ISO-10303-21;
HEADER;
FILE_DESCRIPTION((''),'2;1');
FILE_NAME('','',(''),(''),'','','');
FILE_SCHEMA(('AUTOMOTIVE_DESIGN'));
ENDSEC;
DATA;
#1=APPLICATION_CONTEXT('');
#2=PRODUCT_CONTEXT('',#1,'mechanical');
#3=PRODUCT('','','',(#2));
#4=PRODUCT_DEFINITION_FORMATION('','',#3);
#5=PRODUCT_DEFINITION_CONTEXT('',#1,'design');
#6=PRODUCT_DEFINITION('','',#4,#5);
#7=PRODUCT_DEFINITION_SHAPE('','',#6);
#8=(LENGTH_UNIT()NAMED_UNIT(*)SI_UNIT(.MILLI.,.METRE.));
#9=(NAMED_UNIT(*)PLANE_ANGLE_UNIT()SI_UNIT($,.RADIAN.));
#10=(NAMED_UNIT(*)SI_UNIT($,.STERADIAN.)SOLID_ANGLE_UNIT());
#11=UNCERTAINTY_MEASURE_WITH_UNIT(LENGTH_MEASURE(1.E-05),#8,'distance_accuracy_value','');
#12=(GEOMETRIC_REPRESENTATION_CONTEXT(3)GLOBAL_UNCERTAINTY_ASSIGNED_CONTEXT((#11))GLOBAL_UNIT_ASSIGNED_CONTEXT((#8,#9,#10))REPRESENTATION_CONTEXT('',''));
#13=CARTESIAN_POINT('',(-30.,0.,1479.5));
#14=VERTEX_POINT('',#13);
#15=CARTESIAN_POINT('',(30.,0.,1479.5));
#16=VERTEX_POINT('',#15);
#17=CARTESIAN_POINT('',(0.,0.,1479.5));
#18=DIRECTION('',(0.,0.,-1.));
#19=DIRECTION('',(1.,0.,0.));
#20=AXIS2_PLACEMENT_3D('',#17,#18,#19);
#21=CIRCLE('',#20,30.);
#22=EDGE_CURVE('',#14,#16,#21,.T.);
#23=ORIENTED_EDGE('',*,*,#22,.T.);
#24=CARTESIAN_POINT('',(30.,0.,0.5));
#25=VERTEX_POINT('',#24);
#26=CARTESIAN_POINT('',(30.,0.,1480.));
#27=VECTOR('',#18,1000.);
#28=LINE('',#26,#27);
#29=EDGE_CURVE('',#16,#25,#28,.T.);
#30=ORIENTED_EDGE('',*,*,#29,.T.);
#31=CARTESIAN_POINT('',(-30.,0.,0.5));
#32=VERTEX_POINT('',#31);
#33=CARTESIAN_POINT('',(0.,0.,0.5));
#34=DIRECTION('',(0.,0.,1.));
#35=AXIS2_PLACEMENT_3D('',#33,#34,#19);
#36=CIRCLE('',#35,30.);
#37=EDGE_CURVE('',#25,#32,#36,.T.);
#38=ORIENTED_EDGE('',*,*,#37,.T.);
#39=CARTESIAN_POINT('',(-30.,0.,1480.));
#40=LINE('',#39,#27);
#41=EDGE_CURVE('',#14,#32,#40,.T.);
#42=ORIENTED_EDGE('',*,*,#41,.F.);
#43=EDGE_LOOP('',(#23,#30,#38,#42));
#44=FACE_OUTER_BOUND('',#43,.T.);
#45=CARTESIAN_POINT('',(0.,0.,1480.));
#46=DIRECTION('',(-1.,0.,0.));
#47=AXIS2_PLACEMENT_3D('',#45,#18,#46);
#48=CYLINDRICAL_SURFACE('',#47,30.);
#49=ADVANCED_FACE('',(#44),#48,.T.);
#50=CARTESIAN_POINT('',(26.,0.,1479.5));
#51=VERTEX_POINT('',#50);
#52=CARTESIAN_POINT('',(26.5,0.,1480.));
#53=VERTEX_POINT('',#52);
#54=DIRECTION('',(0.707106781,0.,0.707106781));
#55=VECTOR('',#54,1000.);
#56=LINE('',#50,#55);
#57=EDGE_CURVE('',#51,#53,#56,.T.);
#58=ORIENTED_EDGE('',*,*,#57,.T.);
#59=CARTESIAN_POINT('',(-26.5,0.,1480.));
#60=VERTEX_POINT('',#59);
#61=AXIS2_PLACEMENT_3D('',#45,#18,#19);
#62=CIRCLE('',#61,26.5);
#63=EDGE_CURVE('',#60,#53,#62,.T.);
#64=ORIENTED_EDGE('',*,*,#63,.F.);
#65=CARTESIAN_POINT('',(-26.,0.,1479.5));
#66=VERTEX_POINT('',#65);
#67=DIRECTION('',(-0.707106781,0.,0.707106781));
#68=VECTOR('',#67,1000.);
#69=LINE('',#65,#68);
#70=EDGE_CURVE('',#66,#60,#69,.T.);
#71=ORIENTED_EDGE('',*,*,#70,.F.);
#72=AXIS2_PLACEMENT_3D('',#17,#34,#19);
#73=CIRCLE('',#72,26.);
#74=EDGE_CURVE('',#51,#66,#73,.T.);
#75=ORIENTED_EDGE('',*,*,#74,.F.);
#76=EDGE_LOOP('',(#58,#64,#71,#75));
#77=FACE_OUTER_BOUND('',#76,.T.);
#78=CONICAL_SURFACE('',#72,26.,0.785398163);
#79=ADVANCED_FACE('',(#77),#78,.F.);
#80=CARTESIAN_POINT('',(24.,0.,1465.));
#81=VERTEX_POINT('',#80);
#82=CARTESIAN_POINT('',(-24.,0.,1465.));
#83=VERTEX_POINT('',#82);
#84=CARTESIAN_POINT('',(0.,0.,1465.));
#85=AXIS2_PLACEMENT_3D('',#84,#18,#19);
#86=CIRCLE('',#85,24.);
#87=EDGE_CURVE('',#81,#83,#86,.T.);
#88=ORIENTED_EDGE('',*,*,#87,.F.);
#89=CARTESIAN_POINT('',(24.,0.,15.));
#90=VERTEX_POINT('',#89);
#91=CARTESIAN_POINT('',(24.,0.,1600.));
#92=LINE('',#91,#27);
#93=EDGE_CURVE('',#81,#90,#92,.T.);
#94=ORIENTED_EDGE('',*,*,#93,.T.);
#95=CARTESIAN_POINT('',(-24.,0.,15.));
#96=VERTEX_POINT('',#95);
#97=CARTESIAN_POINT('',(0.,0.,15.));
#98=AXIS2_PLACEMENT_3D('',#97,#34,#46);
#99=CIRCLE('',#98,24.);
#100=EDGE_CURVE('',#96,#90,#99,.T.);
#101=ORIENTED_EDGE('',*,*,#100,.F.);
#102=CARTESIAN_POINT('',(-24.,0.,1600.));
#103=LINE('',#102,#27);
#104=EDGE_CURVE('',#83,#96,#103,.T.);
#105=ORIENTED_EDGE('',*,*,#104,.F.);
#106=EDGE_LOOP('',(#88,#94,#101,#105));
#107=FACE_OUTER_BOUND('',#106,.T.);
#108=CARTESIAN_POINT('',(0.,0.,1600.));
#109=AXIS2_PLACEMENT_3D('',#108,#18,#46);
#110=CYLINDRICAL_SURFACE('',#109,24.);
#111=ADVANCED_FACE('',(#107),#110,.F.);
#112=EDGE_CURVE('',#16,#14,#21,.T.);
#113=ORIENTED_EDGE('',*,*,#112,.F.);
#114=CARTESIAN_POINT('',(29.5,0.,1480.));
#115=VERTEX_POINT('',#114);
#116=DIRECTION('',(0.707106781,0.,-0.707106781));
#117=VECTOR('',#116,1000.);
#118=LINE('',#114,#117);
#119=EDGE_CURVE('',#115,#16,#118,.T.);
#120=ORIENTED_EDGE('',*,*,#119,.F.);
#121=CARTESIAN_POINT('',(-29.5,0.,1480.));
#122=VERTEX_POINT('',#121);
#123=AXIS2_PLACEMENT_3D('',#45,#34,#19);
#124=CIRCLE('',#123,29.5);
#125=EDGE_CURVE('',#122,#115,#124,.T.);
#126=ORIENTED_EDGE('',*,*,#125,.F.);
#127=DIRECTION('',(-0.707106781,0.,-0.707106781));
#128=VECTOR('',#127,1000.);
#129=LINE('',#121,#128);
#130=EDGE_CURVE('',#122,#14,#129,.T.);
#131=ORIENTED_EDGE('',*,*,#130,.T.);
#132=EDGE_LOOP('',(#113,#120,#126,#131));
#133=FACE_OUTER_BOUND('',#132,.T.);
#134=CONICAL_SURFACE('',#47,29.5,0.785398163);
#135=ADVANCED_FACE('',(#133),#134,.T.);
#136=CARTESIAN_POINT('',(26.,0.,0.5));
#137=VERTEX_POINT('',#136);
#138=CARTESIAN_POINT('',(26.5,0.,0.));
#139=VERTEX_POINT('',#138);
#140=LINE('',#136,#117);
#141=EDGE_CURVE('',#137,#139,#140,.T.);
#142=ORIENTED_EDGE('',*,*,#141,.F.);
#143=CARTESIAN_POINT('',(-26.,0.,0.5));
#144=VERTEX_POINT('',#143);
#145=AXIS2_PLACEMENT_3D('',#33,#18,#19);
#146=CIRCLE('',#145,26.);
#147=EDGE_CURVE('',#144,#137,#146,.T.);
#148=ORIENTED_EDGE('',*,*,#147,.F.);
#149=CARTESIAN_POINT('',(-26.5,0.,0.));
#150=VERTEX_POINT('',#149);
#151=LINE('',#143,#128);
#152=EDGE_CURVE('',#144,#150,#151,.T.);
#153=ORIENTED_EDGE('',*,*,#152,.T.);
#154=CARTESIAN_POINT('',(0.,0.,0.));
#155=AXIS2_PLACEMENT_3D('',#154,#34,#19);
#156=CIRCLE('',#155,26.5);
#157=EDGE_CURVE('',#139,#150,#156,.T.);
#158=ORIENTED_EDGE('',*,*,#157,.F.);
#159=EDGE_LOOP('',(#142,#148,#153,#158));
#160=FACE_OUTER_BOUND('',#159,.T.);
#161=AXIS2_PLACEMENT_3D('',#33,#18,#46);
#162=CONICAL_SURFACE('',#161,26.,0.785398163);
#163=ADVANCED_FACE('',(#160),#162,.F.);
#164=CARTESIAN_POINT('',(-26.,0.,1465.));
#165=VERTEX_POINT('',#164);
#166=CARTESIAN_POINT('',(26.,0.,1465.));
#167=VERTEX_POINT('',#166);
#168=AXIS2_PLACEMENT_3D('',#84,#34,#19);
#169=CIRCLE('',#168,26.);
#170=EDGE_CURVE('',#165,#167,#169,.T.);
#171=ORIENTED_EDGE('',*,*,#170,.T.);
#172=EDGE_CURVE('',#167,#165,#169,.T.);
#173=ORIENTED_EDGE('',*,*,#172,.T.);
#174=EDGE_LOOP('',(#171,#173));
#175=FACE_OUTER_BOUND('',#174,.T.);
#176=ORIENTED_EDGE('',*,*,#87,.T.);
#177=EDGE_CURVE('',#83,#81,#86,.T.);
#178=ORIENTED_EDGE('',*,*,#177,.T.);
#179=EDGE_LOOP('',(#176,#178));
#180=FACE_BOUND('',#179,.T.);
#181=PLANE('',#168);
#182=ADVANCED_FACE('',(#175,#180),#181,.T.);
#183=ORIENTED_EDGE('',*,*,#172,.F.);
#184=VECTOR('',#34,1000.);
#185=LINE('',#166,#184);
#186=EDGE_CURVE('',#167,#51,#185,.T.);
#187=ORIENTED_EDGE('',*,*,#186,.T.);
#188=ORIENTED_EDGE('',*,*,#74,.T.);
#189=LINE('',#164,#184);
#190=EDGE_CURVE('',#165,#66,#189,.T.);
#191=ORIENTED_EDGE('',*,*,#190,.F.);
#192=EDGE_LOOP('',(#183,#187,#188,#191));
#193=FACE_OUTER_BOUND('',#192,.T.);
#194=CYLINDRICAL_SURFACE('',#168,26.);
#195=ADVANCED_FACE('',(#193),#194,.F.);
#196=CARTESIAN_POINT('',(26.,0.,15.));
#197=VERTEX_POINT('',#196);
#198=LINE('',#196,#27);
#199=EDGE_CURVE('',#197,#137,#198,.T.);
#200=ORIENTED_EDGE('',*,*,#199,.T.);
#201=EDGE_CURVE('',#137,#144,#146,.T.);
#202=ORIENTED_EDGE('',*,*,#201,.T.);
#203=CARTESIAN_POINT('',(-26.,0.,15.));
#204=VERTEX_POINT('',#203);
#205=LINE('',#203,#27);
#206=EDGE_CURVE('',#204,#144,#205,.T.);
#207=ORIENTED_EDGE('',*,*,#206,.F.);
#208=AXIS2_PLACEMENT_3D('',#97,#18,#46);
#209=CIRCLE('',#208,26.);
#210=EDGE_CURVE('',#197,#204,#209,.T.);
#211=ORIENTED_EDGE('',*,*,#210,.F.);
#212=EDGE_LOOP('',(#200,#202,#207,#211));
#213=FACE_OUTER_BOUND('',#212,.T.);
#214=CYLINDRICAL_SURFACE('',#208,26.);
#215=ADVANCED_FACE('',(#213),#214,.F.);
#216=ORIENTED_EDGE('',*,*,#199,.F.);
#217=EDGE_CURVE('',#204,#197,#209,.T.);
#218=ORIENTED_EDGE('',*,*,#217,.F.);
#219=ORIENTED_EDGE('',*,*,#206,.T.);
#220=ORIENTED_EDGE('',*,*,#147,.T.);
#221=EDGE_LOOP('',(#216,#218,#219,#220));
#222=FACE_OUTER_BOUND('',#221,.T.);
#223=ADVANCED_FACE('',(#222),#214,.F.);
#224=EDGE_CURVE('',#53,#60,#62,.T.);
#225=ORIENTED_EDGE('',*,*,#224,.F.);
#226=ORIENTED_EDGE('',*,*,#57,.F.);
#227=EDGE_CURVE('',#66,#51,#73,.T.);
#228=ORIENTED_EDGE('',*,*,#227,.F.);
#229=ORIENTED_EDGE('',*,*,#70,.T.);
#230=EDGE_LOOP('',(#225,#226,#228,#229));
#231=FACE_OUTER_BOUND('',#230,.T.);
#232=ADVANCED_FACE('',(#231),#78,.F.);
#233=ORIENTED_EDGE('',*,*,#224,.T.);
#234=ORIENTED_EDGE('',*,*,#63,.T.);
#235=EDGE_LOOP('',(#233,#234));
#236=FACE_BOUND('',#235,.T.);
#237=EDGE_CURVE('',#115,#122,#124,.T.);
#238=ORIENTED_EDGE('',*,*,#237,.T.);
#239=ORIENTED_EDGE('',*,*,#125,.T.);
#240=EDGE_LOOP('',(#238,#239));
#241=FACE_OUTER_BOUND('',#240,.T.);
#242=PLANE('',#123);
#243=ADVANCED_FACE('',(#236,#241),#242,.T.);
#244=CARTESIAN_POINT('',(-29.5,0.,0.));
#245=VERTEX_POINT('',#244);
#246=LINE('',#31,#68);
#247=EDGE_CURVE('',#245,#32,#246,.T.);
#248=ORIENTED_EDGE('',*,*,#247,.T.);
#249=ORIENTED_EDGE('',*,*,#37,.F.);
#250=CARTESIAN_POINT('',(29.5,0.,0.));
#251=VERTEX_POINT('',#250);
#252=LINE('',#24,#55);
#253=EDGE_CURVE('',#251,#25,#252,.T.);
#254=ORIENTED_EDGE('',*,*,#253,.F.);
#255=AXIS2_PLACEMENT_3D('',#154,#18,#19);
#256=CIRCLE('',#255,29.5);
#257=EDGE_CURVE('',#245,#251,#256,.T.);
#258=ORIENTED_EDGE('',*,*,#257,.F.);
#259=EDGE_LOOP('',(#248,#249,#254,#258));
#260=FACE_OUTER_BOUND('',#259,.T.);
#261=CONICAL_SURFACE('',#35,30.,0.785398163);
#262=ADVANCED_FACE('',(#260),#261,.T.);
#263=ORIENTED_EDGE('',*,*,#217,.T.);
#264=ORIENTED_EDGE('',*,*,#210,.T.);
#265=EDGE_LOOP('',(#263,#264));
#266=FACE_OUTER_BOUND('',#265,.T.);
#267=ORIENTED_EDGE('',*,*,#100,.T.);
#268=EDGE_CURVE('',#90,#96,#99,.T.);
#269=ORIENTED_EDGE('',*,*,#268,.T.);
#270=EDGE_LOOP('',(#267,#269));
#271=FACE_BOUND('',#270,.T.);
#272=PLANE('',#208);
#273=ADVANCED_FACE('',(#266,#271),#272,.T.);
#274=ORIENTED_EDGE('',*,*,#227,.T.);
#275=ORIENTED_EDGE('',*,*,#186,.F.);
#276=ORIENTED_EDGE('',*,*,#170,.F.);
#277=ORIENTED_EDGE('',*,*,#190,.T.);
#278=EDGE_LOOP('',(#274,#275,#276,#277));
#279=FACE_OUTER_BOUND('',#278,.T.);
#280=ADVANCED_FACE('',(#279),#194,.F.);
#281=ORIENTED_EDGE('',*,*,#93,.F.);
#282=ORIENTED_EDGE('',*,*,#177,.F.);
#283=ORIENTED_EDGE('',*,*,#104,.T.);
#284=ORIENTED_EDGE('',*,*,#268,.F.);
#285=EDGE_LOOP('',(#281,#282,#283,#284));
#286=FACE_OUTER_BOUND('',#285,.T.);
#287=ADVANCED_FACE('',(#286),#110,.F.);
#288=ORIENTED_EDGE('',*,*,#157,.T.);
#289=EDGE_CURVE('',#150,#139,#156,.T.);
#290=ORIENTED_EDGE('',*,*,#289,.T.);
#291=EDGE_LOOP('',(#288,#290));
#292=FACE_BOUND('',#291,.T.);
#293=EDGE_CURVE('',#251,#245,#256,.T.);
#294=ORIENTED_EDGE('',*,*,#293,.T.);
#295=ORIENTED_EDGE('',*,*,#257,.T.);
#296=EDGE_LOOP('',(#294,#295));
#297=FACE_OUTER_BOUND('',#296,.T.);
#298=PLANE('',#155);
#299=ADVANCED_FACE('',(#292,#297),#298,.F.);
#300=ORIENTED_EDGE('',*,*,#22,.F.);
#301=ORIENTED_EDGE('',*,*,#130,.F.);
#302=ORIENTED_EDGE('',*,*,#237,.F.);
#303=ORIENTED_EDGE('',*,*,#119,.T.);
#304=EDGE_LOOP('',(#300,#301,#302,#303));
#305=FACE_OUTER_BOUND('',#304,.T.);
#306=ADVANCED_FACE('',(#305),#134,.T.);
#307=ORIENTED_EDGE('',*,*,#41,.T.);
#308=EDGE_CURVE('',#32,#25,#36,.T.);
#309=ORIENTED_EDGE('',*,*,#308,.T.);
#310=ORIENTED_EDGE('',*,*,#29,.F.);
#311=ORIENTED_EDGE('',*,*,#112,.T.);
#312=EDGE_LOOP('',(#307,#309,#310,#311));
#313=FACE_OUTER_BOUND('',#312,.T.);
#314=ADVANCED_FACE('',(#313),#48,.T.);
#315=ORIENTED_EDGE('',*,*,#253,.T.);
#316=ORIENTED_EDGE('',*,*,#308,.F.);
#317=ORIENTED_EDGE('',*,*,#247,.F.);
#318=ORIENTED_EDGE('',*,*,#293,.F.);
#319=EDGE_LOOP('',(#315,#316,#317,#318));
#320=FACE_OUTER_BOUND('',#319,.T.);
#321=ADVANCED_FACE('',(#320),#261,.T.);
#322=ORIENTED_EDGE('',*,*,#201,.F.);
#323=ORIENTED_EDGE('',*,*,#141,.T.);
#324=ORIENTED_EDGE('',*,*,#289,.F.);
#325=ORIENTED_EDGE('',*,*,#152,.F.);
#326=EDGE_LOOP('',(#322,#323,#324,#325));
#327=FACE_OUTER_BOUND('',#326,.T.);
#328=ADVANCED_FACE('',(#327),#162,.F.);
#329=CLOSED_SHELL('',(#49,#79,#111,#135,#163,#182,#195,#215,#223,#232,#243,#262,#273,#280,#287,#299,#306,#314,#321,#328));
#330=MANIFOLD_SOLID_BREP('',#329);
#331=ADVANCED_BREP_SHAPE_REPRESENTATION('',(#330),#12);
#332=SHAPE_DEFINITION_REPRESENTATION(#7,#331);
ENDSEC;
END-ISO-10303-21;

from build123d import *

# Parameters (mm, degrees)
SKETCH_1_R          = 30
EXTRUDE_1_DEPTH     = 1480
SKETCH_2_R          = 24
CUT_EXTRUDE_1_DEPTH = 1600
SKETCH_3_R          = 26
CUT_EXTRUDE_2_DEPTH = 15
CUT_EXTRUDE_START   = -15
SKETCH_4_R          = 26
CUT_EXTRUDE_3_DEPTH = 15
CHAMFER_1_SIZE      = 0.5


with BuildPart() as part:
    # 草图1 → 凸台-拉伸1 (new body)
    with BuildSketch(Plane.XY):
        Circle(SKETCH_1_R)
    extrude(amount=EXTRUDE_1_DEPTH)

    # 草图2 → 切除-拉伸1 (cut)
    with BuildSketch(Plane(origin=(0, 0, 0), x_dir=(-1, 0, 0), z_dir=(0, 0, -1))):
        Circle(SKETCH_2_R)
    extrude(amount=-CUT_EXTRUDE_1_DEPTH, mode=Mode.SUBTRACT)

    # 草图3 → 切除-拉伸2 (cut)
    with BuildSketch(Plane(origin=(0, 0, 0), x_dir=(-1, 0, 0), z_dir=(0, 0, -1))):
        Circle(SKETCH_3_R)
    extrude(amount=-CUT_EXTRUDE_2_DEPTH, mode=Mode.SUBTRACT)

    # 草图4 → 切除-拉伸3 (cut)
    with BuildSketch(Plane.XY.offset(1480).offset(CUT_EXTRUDE_START)):
        with Locations(Location((0, 0, 0), (0, 0, 180))):
            Circle(SKETCH_4_R)
    extrude(amount=CUT_EXTRUDE_3_DEPTH, mode=Mode.SUBTRACT)

    # 倒角1
    chamfer_1_edges = [part.edges().sort_by_distance(p)[0] for p in [
        (26, 0, 0),
        (-30, 0, 0),
        (26, 0, 1480),
        (-30, 0, 1480),
    ]]
    chamfer(chamfer_1_edges, length=CHAMFER_1_SIZE)


solid = part.part
